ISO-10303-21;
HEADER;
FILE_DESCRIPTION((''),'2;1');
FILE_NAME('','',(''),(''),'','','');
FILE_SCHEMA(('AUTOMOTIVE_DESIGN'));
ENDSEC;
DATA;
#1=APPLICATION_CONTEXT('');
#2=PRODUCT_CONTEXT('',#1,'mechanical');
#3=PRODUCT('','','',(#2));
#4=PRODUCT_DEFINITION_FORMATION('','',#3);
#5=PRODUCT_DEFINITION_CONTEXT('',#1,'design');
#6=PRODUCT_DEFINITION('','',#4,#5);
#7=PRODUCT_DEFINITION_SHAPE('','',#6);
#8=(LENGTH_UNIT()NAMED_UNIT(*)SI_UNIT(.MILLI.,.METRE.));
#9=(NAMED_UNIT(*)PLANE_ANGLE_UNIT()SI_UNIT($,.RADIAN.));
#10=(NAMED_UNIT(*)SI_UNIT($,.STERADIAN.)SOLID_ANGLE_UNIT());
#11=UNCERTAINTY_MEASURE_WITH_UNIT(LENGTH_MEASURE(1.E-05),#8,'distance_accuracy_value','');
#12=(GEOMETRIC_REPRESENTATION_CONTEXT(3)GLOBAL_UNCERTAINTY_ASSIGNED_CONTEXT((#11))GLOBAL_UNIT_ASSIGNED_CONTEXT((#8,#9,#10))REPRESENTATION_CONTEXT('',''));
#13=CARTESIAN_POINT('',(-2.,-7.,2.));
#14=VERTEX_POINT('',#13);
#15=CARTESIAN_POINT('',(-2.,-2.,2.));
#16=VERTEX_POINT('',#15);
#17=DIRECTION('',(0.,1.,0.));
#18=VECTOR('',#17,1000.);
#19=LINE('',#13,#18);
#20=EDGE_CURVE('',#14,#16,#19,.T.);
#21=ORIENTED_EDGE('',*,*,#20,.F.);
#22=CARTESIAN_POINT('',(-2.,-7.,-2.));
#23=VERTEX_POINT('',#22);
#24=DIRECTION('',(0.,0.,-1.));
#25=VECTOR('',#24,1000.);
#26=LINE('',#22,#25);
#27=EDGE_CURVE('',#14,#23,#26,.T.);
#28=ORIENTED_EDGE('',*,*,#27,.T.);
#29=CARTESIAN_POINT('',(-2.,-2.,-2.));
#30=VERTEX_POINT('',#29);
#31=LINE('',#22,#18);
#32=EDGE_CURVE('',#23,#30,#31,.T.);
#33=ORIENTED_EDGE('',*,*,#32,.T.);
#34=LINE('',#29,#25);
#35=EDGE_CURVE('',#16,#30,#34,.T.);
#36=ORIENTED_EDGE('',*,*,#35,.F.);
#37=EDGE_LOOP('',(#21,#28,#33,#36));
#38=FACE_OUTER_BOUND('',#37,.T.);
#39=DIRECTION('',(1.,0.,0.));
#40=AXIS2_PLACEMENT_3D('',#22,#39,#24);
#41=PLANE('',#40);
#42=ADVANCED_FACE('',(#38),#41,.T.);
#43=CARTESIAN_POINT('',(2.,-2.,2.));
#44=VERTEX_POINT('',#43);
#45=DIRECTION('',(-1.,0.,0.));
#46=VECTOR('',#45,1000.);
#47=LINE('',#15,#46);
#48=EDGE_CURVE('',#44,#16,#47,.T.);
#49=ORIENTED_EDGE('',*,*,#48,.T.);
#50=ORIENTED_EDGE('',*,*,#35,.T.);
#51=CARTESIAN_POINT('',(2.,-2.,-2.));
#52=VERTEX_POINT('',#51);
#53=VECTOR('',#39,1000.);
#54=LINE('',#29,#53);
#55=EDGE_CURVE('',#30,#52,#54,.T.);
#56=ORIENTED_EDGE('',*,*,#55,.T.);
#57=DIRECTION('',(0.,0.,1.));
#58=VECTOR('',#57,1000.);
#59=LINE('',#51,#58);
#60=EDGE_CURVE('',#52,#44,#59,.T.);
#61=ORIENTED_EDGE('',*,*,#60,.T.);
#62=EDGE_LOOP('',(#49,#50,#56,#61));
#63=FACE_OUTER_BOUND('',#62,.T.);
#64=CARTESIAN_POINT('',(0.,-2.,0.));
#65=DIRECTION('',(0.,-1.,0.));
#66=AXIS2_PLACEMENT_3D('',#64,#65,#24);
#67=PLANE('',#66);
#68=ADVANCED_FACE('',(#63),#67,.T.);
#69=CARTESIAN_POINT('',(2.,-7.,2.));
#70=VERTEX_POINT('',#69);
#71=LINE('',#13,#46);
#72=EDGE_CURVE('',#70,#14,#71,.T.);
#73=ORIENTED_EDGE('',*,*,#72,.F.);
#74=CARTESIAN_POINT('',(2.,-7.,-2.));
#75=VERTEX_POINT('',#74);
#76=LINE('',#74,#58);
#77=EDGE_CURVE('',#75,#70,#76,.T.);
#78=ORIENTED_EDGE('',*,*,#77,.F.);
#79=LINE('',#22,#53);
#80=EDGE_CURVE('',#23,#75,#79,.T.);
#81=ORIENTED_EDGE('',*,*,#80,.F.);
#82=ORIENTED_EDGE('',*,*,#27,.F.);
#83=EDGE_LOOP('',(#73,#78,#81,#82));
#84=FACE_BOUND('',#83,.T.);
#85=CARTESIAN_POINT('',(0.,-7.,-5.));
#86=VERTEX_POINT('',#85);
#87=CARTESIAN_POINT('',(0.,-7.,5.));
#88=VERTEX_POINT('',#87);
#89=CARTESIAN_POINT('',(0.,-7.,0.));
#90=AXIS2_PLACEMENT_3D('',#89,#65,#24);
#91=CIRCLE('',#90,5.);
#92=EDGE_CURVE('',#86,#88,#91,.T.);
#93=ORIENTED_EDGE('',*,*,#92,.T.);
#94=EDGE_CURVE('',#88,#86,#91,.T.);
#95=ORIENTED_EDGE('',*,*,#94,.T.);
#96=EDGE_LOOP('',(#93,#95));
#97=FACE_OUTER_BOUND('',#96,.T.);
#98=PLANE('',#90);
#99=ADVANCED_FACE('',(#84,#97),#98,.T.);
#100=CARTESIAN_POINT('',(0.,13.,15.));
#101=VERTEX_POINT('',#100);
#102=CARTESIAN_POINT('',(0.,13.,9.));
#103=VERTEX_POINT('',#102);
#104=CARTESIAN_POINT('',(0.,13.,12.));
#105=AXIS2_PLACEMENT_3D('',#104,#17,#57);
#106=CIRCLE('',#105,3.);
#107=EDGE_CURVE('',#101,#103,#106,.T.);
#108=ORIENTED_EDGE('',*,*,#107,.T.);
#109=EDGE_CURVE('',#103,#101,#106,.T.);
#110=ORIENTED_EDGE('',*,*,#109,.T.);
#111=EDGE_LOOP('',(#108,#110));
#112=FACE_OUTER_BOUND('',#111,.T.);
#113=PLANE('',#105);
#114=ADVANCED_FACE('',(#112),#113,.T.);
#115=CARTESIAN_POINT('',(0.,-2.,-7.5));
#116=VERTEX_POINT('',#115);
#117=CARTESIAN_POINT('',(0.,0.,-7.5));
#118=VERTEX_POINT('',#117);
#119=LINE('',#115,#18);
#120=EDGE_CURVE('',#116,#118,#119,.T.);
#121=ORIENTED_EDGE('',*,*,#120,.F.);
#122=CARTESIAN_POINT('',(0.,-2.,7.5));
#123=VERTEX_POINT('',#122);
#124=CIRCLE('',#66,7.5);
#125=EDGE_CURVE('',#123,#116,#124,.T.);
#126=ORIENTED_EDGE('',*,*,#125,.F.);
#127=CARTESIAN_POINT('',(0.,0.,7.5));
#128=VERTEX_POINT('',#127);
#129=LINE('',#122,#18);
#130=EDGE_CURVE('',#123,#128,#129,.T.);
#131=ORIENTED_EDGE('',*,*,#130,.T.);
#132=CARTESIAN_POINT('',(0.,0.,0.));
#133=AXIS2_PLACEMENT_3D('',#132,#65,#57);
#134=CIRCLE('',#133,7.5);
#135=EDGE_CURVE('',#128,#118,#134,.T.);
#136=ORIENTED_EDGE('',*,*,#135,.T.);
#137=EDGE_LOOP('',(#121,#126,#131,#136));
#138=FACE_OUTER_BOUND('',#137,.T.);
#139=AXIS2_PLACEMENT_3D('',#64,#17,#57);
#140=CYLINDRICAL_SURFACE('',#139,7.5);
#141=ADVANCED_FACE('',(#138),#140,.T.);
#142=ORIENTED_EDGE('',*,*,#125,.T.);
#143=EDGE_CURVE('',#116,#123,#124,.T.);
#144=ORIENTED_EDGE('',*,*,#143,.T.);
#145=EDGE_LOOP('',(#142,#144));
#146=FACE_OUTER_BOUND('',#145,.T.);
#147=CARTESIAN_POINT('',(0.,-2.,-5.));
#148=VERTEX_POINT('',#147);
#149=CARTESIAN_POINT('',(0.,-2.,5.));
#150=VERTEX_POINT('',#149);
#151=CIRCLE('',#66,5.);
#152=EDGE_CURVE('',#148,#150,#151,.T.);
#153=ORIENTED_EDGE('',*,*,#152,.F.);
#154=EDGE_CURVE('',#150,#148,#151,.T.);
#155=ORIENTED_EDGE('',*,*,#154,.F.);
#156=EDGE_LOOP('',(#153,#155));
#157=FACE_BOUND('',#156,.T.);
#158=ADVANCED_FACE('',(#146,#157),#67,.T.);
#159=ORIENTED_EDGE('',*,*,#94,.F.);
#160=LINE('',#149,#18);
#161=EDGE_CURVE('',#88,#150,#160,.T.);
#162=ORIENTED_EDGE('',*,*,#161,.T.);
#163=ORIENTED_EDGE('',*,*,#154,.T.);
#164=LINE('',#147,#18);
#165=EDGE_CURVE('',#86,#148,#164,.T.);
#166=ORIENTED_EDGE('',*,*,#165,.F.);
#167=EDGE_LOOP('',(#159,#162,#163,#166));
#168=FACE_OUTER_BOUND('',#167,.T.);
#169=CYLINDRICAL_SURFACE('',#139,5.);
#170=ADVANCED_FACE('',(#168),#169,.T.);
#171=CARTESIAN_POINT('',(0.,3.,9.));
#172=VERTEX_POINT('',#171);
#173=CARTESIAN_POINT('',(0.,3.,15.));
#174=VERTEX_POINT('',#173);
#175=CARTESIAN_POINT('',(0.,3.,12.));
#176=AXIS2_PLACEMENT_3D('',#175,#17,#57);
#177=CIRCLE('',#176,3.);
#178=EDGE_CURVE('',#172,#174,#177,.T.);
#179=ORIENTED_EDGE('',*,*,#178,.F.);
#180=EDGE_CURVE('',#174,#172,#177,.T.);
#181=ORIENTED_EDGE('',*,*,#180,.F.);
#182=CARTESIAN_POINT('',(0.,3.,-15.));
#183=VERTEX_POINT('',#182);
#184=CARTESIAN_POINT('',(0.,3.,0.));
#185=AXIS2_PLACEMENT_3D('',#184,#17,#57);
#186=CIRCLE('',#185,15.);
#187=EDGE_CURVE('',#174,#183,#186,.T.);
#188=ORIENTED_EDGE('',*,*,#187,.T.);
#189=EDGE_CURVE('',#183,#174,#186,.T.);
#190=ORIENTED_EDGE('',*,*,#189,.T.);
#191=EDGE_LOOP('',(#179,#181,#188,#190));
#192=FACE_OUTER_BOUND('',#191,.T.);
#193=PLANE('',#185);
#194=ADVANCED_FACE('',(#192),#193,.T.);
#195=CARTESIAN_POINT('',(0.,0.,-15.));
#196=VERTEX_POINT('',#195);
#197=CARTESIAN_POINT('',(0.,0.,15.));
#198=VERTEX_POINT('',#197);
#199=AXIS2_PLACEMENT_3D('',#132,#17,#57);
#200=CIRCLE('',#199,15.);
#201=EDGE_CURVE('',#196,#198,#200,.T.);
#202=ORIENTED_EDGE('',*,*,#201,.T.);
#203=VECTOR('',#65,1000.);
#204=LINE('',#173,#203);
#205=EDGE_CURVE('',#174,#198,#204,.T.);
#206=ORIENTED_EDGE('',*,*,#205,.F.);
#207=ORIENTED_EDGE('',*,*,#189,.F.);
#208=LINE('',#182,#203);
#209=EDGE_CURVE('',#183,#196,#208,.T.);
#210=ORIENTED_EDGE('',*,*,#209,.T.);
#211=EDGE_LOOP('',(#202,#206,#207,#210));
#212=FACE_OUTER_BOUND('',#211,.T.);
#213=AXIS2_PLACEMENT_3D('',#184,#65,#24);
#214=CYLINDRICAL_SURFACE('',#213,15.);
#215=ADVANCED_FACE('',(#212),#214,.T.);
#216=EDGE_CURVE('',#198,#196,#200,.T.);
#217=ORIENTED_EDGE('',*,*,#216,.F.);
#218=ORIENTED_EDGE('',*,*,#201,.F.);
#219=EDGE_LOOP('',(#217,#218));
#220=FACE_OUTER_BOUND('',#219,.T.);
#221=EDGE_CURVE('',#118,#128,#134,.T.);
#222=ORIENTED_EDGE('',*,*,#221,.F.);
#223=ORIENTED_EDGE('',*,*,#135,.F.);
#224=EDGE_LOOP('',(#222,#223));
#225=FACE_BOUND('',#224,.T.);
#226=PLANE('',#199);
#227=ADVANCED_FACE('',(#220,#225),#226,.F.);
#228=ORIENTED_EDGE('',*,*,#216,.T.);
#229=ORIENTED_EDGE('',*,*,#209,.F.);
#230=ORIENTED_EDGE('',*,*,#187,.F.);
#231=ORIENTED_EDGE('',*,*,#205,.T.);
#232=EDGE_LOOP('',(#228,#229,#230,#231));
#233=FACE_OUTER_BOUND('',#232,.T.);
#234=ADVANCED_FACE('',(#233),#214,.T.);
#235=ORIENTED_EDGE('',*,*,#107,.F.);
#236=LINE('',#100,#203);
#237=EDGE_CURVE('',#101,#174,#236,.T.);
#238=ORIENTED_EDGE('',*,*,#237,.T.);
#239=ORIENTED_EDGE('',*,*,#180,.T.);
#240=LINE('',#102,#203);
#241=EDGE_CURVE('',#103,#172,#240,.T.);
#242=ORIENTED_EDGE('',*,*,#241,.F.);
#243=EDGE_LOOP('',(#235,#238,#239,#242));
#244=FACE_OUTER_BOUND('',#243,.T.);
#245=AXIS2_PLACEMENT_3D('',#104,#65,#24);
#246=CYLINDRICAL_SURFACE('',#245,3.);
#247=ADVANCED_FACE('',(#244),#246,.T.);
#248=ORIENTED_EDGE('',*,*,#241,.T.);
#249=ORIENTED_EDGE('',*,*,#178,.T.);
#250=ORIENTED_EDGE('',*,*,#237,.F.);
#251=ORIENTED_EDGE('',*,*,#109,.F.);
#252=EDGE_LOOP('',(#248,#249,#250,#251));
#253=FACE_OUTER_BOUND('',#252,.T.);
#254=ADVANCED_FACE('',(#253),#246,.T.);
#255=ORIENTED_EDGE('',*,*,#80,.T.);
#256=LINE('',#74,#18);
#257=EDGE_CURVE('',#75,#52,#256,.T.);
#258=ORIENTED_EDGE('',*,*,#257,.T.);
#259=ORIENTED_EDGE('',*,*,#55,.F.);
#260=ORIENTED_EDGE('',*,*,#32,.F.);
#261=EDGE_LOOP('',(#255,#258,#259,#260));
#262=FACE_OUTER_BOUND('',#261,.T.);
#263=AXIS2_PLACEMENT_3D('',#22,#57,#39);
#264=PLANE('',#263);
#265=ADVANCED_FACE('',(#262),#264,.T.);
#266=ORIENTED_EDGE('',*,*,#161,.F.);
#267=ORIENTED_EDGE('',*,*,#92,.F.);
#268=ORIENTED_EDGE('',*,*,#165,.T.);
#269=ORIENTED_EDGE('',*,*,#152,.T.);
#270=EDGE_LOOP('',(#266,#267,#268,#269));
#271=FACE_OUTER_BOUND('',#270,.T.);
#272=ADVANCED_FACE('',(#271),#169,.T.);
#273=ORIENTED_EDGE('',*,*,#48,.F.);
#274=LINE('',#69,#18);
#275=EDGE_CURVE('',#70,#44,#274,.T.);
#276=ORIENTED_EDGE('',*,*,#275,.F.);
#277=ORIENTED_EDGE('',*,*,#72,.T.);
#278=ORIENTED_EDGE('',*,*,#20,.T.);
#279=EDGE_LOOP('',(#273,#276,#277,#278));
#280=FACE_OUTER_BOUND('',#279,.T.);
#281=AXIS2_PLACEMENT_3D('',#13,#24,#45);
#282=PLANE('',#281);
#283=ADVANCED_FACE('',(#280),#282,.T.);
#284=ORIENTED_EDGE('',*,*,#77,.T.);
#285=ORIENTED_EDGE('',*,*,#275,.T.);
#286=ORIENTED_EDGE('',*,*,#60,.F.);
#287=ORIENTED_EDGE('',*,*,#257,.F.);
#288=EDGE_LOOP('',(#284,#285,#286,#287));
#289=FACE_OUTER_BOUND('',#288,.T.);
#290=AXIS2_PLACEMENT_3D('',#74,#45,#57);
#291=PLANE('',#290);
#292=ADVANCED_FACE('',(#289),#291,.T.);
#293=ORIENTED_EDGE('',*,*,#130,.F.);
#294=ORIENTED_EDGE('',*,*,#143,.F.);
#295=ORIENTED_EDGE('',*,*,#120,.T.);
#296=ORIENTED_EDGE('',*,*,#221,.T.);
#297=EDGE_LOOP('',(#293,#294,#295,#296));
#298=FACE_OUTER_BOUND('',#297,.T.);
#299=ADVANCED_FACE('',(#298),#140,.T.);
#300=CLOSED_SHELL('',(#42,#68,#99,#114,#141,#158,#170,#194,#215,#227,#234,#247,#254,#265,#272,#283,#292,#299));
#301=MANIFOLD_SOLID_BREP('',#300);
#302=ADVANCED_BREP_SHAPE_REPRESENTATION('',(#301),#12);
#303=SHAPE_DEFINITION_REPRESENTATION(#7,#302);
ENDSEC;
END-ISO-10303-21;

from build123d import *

# Parameters (mm, degrees)
SKETCH1_R           = 15
BOSS_EXTRUDE1_DEPTH = 3
SKETCH2_R           = 3
BOSS_EXTRUDE2_DEPTH = 10
SKETCH3_R           = 5
BOSS_EXTRUDE3_DEPTH = 2
SKETCH4_R           = 5
SKETCH4_W           = 4
SKETCH4_H           = 4
BOSS_EXTRUDE4_DEPTH = 5
SKETCH5_R           = 7.5
BOSS_EXTRUDE5_DEPTH = 2


with BuildPart() as part:
    # Sketch1 → Boss-Extrude1 (new body)
    with BuildSketch(Plane(origin=(0, 0, 0), x_dir=(1, 0, 0), z_dir=(0, 1, 0))):
        with Locations(Location((0, 0, 0), (0, 0, 270))):
            Circle(SKETCH1_R)
    extrude(amount=BOSS_EXTRUDE1_DEPTH)

    # Sketch2 → Boss-Extrude2 (add)
    with BuildSketch(Plane(origin=(0, 3, 0), x_dir=(1, 0, 0), z_dir=(0, 1, 0))):
        with Locations(Location((0, -12, 0), (0, 0, 270))):
            Circle(SKETCH2_R)
    extrude(amount=BOSS_EXTRUDE2_DEPTH)

    # Sketch3 → Boss-Extrude3 (add)
    with BuildSketch(Plane(origin=(0, 0, 0), x_dir=(-1, 0, 0), z_dir=(0, -1, 0))):
        with Locations(Location((0, 0, 0), (0, 0, 90))):
            Circle(SKETCH3_R)
    extrude(amount=BOSS_EXTRUDE3_DEPTH)

    # Sketch4 → Boss-Extrude4 (add)
    with BuildSketch(Plane(origin=(0, -2, 0), x_dir=(-1, 0, 0), z_dir=(0, -1, 0))):
        with Locations(Location((0, 0, 0), (0, 0, 90))):
            Circle(SKETCH4_R)
        Rectangle(SKETCH4_W, SKETCH4_H, mode=Mode.SUBTRACT)
    extrude(amount=BOSS_EXTRUDE4_DEPTH)

    # Sketch5 → Boss-Extrude5 (add)
    with BuildSketch(Plane(origin=(0, 0, 0), x_dir=(-1, 0, 0), z_dir=(0, -1, 0))):
        with Locations(Location((0, 0, 0), (0, 0, 270))):
            Circle(SKETCH5_R)
    extrude(amount=BOSS_EXTRUDE5_DEPTH)


solid = part.part
